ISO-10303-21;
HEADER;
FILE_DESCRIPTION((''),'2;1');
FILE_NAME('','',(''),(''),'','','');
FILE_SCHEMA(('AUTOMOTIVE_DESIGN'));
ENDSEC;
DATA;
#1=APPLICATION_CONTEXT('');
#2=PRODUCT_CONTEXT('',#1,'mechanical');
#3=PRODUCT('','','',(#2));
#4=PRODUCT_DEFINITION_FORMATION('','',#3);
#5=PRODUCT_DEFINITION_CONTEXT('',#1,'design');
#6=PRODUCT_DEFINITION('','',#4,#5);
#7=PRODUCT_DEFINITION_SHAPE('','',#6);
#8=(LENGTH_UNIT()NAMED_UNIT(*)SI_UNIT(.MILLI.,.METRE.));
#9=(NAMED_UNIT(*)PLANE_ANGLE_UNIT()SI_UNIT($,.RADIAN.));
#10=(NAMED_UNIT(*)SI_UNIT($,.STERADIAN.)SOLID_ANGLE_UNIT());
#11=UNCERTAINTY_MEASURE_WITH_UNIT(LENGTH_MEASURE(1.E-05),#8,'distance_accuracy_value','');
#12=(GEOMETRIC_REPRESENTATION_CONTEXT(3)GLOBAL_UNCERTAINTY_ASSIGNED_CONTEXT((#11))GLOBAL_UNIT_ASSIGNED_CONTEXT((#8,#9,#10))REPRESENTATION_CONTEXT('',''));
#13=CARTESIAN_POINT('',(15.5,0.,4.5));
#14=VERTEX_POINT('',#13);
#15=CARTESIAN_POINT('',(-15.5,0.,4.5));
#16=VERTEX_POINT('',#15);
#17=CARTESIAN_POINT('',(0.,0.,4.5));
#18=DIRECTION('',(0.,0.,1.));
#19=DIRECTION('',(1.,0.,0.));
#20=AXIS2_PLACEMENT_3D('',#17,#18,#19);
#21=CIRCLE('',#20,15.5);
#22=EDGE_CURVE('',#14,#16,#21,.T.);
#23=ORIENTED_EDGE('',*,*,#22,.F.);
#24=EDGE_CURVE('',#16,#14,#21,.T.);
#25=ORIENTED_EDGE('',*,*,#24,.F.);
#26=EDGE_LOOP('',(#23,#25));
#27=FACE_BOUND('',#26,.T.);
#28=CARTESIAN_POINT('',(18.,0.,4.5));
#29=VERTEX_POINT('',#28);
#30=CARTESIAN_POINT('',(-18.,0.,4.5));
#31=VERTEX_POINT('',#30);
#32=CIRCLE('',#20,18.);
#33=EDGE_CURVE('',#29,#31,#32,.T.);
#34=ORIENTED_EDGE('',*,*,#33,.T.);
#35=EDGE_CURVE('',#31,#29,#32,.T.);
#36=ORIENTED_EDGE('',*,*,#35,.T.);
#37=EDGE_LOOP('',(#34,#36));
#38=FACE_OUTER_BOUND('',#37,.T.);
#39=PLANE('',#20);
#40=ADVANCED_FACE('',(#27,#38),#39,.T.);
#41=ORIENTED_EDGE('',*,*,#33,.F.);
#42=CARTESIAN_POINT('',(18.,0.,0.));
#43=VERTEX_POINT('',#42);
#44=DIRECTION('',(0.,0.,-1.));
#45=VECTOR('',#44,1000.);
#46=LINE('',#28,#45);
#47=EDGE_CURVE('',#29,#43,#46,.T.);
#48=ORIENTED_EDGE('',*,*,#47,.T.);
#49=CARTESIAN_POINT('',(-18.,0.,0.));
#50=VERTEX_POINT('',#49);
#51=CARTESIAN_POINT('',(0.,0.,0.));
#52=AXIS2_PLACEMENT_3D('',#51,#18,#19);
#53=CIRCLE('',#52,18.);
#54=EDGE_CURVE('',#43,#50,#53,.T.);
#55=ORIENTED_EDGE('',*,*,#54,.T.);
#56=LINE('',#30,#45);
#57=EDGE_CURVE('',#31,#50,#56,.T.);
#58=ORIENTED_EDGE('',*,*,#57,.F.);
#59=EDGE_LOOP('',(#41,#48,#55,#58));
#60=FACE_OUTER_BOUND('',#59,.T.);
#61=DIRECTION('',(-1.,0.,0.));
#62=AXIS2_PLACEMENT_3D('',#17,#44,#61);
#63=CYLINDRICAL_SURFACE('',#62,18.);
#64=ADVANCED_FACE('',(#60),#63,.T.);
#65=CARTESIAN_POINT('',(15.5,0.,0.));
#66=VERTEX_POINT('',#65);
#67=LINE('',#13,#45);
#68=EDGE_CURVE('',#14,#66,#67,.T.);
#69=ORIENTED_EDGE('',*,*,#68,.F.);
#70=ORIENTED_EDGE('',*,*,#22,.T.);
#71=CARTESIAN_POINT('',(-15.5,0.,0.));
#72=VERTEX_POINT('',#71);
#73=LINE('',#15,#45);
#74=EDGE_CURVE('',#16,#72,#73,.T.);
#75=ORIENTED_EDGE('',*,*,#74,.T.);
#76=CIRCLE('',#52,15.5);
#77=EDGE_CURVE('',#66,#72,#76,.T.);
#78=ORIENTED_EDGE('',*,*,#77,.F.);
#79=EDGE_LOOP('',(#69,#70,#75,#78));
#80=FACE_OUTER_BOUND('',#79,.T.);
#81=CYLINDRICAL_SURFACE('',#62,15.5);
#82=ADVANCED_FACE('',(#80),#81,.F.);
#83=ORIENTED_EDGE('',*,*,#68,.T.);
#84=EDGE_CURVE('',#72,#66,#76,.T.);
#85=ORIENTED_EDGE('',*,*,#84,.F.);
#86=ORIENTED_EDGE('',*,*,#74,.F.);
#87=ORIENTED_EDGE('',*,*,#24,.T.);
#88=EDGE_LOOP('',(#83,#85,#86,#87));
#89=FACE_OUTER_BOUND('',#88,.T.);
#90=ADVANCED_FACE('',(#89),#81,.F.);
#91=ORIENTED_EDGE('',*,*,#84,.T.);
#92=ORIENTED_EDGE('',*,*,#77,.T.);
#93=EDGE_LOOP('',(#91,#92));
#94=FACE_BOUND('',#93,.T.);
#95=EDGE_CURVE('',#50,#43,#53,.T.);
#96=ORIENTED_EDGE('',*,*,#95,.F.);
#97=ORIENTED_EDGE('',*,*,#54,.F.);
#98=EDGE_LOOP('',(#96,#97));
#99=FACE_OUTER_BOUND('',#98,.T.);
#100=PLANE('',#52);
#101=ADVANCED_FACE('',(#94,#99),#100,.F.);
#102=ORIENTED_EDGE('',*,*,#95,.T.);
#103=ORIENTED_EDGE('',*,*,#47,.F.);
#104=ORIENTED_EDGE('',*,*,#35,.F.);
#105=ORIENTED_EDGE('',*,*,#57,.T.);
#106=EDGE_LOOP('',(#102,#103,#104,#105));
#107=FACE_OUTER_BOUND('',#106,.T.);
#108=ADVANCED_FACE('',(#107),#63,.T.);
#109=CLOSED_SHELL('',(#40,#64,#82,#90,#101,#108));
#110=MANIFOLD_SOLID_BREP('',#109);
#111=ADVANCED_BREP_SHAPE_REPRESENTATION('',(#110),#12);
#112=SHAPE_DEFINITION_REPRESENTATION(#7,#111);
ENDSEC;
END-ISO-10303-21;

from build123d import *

# Parameters (mm, degrees)
SKETCH_1_R      = 18
SKETCH_1_R_2    = 15.5
EXTRUDE_1_DEPTH = 4.5


with BuildPart() as part:
    # 草图1 → 凸台-拉伸1 (new body)
    with BuildSketch(Plane.XY):
        Circle(SKETCH_1_R)
        Circle(SKETCH_1_R_2, mode=Mode.SUBTRACT)
    extrude(amount=EXTRUDE_1_DEPTH)


solid = part.part
